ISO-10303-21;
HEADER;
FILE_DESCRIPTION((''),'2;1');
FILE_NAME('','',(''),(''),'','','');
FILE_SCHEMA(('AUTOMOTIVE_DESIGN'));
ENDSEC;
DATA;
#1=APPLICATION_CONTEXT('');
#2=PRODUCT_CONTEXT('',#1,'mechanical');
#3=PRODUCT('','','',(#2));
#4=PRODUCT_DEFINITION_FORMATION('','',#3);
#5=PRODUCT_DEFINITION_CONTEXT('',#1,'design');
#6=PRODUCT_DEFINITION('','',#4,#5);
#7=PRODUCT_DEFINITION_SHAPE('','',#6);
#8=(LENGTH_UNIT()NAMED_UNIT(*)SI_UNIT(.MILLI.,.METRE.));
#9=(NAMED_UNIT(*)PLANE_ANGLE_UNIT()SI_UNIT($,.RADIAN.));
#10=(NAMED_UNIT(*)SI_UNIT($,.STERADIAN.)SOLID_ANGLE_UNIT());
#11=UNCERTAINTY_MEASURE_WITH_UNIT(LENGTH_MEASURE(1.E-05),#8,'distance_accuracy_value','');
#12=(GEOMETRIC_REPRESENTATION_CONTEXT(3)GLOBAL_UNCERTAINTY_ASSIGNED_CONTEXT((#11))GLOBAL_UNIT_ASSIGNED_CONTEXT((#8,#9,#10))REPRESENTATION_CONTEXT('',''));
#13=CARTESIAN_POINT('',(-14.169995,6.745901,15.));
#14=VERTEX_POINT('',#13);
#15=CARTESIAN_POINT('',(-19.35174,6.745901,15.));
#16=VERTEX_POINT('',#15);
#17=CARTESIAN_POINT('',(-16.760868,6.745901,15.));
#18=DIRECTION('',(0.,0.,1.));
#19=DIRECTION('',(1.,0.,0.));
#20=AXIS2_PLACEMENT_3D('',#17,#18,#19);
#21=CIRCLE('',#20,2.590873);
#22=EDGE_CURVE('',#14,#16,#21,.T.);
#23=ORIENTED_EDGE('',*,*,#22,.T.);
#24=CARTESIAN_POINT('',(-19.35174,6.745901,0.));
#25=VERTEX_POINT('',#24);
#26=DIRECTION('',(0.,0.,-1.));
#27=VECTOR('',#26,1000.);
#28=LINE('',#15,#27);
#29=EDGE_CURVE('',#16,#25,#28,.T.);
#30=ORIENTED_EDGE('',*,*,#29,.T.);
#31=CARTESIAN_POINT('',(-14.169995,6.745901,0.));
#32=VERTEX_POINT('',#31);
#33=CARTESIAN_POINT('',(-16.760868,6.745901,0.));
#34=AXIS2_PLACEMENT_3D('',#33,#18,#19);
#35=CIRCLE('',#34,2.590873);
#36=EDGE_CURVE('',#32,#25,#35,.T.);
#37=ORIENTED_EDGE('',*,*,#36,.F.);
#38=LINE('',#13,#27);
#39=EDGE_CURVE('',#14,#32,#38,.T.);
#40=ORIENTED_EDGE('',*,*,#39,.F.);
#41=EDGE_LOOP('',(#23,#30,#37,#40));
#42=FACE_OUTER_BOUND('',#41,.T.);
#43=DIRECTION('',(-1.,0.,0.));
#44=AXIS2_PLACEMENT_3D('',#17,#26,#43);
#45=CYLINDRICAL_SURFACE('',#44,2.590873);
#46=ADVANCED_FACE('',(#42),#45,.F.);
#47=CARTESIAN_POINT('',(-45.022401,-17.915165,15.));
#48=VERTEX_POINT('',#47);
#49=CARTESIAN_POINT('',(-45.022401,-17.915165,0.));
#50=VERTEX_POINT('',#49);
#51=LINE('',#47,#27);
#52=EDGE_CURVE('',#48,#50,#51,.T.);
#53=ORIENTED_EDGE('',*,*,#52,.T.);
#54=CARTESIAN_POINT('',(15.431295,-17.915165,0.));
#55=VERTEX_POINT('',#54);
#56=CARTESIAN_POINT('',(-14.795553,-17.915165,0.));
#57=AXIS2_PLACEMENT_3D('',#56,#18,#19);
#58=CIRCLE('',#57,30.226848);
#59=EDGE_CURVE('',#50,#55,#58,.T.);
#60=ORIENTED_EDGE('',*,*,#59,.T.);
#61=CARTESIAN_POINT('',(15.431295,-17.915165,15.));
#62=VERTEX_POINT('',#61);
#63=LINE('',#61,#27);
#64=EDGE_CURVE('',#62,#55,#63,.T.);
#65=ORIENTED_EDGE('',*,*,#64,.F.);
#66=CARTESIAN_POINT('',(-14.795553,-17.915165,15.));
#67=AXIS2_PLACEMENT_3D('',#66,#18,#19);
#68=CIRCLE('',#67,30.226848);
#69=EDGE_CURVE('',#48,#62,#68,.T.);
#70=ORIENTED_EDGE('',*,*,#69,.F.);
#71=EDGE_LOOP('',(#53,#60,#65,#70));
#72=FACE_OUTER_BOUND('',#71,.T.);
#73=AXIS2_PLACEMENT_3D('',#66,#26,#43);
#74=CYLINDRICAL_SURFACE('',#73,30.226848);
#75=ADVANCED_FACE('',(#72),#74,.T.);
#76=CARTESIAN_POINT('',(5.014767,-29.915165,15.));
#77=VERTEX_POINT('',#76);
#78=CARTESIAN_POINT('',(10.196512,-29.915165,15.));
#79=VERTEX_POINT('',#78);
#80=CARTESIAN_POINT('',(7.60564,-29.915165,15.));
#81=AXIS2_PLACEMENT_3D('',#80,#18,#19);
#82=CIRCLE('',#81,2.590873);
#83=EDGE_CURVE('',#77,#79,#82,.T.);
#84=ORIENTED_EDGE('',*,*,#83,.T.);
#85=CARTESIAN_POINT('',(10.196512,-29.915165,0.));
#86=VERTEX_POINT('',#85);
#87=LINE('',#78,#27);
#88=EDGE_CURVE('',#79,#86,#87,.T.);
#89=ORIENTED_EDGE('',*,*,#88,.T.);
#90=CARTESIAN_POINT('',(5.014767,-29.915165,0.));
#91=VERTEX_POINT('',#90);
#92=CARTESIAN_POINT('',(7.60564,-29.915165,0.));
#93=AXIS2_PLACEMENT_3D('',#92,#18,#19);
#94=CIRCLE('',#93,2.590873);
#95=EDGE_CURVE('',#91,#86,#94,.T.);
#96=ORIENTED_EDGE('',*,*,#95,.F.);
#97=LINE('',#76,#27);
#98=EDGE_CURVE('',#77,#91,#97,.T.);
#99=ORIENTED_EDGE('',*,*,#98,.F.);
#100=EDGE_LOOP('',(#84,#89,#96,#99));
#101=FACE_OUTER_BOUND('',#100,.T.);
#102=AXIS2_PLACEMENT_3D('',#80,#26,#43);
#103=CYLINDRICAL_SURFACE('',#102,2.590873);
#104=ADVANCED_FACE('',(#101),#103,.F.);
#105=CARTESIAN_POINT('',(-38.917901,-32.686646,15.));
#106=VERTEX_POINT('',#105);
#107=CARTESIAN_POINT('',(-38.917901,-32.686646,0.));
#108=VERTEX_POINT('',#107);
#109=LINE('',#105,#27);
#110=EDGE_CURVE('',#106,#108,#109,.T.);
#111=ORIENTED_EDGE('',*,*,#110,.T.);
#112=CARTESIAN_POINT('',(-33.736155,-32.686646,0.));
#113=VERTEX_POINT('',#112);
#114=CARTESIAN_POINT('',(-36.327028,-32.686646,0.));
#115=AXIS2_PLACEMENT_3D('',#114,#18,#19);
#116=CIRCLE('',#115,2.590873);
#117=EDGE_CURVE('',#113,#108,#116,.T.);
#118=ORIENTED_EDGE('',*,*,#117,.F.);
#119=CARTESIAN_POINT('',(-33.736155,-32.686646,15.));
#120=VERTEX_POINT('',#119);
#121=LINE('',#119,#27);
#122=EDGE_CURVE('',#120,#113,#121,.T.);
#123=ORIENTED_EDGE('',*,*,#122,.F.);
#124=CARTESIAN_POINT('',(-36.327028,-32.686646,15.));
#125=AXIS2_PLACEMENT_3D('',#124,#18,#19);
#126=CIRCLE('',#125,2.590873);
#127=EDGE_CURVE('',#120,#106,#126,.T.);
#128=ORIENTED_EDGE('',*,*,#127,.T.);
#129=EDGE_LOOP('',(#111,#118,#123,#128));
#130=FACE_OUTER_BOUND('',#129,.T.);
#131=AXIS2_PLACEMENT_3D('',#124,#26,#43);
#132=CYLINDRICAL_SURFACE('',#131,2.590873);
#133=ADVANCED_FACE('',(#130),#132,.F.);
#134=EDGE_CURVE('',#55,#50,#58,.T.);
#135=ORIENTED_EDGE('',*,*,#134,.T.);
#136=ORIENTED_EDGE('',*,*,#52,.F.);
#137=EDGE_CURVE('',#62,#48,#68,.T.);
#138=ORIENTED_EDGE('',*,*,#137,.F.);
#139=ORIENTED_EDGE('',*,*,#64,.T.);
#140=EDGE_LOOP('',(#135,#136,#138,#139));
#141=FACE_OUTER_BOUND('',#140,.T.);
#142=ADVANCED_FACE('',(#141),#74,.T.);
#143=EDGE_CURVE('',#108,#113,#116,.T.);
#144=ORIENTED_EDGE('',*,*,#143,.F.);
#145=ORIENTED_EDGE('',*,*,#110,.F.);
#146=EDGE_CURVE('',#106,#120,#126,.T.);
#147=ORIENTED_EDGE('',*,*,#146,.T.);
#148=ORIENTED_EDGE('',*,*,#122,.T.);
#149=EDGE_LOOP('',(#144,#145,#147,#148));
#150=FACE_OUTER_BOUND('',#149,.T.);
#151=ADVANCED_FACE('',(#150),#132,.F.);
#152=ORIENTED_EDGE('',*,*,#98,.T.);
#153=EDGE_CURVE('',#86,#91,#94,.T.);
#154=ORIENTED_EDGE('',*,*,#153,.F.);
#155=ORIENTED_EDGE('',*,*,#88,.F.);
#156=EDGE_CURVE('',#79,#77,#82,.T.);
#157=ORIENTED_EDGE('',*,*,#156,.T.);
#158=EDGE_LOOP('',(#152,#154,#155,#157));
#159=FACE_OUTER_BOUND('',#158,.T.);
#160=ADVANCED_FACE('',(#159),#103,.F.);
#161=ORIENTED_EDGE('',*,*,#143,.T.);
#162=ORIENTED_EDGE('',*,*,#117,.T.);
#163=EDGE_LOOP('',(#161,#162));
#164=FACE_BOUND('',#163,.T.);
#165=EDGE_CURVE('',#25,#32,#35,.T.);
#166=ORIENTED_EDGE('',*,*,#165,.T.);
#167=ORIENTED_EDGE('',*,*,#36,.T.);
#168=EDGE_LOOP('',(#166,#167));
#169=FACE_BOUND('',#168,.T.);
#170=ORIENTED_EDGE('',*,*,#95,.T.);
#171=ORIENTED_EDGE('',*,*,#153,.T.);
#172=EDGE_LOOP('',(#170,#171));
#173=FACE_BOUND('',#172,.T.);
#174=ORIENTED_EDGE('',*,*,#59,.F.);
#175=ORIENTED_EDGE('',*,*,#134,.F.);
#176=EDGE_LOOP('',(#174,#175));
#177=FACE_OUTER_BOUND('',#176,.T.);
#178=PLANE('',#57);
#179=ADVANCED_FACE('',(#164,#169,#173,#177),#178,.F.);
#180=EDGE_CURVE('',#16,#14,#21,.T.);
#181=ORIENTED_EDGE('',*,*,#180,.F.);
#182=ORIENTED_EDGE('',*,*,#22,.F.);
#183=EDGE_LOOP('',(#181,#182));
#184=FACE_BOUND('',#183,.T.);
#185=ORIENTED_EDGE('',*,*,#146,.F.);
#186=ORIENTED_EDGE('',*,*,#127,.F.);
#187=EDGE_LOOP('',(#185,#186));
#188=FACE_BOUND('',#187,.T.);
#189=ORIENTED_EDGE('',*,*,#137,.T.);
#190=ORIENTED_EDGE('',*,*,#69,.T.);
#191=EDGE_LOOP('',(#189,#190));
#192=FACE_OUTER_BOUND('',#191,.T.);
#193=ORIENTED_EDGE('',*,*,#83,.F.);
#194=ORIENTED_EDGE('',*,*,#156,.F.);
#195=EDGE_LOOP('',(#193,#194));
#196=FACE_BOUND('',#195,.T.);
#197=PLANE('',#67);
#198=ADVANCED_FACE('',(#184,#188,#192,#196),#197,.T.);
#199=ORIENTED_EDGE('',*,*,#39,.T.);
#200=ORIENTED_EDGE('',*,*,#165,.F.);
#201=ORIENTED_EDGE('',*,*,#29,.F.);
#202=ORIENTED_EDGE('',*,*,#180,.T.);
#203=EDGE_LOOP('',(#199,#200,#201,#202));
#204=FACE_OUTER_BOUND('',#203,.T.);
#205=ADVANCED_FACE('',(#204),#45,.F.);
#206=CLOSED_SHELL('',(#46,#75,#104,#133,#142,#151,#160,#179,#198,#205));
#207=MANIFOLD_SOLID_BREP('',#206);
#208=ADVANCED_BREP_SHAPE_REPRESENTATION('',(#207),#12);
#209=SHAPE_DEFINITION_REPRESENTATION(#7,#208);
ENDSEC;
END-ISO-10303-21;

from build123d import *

# Parameters (mm, degrees)
MODEL_R             = 30.226848254
MODEL_R_2           = 2.590872707
BOSS_EXTRUDE1_DEPTH = 15


with BuildPart() as part:
    # Model → Boss-Extrude1 (new body)
    with BuildSketch(Plane.XY):
        with Locations((-14.795552969, -17.915164858)):
            Circle(MODEL_R)
        with Locations((-16.760867787, 6.745900605)):
            Circle(MODEL_R_2, mode=Mode.SUBTRACT)
        with Locations((-36.327028146, -32.68664647)):
            Circle(MODEL_R_2, mode=Mode.SUBTRACT)
        with Locations((7.605639537, -29.915164858)):
            Circle(MODEL_R_2, mode=Mode.SUBTRACT)
    extrude(amount=BOSS_EXTRUDE1_DEPTH)


solid = part.part
